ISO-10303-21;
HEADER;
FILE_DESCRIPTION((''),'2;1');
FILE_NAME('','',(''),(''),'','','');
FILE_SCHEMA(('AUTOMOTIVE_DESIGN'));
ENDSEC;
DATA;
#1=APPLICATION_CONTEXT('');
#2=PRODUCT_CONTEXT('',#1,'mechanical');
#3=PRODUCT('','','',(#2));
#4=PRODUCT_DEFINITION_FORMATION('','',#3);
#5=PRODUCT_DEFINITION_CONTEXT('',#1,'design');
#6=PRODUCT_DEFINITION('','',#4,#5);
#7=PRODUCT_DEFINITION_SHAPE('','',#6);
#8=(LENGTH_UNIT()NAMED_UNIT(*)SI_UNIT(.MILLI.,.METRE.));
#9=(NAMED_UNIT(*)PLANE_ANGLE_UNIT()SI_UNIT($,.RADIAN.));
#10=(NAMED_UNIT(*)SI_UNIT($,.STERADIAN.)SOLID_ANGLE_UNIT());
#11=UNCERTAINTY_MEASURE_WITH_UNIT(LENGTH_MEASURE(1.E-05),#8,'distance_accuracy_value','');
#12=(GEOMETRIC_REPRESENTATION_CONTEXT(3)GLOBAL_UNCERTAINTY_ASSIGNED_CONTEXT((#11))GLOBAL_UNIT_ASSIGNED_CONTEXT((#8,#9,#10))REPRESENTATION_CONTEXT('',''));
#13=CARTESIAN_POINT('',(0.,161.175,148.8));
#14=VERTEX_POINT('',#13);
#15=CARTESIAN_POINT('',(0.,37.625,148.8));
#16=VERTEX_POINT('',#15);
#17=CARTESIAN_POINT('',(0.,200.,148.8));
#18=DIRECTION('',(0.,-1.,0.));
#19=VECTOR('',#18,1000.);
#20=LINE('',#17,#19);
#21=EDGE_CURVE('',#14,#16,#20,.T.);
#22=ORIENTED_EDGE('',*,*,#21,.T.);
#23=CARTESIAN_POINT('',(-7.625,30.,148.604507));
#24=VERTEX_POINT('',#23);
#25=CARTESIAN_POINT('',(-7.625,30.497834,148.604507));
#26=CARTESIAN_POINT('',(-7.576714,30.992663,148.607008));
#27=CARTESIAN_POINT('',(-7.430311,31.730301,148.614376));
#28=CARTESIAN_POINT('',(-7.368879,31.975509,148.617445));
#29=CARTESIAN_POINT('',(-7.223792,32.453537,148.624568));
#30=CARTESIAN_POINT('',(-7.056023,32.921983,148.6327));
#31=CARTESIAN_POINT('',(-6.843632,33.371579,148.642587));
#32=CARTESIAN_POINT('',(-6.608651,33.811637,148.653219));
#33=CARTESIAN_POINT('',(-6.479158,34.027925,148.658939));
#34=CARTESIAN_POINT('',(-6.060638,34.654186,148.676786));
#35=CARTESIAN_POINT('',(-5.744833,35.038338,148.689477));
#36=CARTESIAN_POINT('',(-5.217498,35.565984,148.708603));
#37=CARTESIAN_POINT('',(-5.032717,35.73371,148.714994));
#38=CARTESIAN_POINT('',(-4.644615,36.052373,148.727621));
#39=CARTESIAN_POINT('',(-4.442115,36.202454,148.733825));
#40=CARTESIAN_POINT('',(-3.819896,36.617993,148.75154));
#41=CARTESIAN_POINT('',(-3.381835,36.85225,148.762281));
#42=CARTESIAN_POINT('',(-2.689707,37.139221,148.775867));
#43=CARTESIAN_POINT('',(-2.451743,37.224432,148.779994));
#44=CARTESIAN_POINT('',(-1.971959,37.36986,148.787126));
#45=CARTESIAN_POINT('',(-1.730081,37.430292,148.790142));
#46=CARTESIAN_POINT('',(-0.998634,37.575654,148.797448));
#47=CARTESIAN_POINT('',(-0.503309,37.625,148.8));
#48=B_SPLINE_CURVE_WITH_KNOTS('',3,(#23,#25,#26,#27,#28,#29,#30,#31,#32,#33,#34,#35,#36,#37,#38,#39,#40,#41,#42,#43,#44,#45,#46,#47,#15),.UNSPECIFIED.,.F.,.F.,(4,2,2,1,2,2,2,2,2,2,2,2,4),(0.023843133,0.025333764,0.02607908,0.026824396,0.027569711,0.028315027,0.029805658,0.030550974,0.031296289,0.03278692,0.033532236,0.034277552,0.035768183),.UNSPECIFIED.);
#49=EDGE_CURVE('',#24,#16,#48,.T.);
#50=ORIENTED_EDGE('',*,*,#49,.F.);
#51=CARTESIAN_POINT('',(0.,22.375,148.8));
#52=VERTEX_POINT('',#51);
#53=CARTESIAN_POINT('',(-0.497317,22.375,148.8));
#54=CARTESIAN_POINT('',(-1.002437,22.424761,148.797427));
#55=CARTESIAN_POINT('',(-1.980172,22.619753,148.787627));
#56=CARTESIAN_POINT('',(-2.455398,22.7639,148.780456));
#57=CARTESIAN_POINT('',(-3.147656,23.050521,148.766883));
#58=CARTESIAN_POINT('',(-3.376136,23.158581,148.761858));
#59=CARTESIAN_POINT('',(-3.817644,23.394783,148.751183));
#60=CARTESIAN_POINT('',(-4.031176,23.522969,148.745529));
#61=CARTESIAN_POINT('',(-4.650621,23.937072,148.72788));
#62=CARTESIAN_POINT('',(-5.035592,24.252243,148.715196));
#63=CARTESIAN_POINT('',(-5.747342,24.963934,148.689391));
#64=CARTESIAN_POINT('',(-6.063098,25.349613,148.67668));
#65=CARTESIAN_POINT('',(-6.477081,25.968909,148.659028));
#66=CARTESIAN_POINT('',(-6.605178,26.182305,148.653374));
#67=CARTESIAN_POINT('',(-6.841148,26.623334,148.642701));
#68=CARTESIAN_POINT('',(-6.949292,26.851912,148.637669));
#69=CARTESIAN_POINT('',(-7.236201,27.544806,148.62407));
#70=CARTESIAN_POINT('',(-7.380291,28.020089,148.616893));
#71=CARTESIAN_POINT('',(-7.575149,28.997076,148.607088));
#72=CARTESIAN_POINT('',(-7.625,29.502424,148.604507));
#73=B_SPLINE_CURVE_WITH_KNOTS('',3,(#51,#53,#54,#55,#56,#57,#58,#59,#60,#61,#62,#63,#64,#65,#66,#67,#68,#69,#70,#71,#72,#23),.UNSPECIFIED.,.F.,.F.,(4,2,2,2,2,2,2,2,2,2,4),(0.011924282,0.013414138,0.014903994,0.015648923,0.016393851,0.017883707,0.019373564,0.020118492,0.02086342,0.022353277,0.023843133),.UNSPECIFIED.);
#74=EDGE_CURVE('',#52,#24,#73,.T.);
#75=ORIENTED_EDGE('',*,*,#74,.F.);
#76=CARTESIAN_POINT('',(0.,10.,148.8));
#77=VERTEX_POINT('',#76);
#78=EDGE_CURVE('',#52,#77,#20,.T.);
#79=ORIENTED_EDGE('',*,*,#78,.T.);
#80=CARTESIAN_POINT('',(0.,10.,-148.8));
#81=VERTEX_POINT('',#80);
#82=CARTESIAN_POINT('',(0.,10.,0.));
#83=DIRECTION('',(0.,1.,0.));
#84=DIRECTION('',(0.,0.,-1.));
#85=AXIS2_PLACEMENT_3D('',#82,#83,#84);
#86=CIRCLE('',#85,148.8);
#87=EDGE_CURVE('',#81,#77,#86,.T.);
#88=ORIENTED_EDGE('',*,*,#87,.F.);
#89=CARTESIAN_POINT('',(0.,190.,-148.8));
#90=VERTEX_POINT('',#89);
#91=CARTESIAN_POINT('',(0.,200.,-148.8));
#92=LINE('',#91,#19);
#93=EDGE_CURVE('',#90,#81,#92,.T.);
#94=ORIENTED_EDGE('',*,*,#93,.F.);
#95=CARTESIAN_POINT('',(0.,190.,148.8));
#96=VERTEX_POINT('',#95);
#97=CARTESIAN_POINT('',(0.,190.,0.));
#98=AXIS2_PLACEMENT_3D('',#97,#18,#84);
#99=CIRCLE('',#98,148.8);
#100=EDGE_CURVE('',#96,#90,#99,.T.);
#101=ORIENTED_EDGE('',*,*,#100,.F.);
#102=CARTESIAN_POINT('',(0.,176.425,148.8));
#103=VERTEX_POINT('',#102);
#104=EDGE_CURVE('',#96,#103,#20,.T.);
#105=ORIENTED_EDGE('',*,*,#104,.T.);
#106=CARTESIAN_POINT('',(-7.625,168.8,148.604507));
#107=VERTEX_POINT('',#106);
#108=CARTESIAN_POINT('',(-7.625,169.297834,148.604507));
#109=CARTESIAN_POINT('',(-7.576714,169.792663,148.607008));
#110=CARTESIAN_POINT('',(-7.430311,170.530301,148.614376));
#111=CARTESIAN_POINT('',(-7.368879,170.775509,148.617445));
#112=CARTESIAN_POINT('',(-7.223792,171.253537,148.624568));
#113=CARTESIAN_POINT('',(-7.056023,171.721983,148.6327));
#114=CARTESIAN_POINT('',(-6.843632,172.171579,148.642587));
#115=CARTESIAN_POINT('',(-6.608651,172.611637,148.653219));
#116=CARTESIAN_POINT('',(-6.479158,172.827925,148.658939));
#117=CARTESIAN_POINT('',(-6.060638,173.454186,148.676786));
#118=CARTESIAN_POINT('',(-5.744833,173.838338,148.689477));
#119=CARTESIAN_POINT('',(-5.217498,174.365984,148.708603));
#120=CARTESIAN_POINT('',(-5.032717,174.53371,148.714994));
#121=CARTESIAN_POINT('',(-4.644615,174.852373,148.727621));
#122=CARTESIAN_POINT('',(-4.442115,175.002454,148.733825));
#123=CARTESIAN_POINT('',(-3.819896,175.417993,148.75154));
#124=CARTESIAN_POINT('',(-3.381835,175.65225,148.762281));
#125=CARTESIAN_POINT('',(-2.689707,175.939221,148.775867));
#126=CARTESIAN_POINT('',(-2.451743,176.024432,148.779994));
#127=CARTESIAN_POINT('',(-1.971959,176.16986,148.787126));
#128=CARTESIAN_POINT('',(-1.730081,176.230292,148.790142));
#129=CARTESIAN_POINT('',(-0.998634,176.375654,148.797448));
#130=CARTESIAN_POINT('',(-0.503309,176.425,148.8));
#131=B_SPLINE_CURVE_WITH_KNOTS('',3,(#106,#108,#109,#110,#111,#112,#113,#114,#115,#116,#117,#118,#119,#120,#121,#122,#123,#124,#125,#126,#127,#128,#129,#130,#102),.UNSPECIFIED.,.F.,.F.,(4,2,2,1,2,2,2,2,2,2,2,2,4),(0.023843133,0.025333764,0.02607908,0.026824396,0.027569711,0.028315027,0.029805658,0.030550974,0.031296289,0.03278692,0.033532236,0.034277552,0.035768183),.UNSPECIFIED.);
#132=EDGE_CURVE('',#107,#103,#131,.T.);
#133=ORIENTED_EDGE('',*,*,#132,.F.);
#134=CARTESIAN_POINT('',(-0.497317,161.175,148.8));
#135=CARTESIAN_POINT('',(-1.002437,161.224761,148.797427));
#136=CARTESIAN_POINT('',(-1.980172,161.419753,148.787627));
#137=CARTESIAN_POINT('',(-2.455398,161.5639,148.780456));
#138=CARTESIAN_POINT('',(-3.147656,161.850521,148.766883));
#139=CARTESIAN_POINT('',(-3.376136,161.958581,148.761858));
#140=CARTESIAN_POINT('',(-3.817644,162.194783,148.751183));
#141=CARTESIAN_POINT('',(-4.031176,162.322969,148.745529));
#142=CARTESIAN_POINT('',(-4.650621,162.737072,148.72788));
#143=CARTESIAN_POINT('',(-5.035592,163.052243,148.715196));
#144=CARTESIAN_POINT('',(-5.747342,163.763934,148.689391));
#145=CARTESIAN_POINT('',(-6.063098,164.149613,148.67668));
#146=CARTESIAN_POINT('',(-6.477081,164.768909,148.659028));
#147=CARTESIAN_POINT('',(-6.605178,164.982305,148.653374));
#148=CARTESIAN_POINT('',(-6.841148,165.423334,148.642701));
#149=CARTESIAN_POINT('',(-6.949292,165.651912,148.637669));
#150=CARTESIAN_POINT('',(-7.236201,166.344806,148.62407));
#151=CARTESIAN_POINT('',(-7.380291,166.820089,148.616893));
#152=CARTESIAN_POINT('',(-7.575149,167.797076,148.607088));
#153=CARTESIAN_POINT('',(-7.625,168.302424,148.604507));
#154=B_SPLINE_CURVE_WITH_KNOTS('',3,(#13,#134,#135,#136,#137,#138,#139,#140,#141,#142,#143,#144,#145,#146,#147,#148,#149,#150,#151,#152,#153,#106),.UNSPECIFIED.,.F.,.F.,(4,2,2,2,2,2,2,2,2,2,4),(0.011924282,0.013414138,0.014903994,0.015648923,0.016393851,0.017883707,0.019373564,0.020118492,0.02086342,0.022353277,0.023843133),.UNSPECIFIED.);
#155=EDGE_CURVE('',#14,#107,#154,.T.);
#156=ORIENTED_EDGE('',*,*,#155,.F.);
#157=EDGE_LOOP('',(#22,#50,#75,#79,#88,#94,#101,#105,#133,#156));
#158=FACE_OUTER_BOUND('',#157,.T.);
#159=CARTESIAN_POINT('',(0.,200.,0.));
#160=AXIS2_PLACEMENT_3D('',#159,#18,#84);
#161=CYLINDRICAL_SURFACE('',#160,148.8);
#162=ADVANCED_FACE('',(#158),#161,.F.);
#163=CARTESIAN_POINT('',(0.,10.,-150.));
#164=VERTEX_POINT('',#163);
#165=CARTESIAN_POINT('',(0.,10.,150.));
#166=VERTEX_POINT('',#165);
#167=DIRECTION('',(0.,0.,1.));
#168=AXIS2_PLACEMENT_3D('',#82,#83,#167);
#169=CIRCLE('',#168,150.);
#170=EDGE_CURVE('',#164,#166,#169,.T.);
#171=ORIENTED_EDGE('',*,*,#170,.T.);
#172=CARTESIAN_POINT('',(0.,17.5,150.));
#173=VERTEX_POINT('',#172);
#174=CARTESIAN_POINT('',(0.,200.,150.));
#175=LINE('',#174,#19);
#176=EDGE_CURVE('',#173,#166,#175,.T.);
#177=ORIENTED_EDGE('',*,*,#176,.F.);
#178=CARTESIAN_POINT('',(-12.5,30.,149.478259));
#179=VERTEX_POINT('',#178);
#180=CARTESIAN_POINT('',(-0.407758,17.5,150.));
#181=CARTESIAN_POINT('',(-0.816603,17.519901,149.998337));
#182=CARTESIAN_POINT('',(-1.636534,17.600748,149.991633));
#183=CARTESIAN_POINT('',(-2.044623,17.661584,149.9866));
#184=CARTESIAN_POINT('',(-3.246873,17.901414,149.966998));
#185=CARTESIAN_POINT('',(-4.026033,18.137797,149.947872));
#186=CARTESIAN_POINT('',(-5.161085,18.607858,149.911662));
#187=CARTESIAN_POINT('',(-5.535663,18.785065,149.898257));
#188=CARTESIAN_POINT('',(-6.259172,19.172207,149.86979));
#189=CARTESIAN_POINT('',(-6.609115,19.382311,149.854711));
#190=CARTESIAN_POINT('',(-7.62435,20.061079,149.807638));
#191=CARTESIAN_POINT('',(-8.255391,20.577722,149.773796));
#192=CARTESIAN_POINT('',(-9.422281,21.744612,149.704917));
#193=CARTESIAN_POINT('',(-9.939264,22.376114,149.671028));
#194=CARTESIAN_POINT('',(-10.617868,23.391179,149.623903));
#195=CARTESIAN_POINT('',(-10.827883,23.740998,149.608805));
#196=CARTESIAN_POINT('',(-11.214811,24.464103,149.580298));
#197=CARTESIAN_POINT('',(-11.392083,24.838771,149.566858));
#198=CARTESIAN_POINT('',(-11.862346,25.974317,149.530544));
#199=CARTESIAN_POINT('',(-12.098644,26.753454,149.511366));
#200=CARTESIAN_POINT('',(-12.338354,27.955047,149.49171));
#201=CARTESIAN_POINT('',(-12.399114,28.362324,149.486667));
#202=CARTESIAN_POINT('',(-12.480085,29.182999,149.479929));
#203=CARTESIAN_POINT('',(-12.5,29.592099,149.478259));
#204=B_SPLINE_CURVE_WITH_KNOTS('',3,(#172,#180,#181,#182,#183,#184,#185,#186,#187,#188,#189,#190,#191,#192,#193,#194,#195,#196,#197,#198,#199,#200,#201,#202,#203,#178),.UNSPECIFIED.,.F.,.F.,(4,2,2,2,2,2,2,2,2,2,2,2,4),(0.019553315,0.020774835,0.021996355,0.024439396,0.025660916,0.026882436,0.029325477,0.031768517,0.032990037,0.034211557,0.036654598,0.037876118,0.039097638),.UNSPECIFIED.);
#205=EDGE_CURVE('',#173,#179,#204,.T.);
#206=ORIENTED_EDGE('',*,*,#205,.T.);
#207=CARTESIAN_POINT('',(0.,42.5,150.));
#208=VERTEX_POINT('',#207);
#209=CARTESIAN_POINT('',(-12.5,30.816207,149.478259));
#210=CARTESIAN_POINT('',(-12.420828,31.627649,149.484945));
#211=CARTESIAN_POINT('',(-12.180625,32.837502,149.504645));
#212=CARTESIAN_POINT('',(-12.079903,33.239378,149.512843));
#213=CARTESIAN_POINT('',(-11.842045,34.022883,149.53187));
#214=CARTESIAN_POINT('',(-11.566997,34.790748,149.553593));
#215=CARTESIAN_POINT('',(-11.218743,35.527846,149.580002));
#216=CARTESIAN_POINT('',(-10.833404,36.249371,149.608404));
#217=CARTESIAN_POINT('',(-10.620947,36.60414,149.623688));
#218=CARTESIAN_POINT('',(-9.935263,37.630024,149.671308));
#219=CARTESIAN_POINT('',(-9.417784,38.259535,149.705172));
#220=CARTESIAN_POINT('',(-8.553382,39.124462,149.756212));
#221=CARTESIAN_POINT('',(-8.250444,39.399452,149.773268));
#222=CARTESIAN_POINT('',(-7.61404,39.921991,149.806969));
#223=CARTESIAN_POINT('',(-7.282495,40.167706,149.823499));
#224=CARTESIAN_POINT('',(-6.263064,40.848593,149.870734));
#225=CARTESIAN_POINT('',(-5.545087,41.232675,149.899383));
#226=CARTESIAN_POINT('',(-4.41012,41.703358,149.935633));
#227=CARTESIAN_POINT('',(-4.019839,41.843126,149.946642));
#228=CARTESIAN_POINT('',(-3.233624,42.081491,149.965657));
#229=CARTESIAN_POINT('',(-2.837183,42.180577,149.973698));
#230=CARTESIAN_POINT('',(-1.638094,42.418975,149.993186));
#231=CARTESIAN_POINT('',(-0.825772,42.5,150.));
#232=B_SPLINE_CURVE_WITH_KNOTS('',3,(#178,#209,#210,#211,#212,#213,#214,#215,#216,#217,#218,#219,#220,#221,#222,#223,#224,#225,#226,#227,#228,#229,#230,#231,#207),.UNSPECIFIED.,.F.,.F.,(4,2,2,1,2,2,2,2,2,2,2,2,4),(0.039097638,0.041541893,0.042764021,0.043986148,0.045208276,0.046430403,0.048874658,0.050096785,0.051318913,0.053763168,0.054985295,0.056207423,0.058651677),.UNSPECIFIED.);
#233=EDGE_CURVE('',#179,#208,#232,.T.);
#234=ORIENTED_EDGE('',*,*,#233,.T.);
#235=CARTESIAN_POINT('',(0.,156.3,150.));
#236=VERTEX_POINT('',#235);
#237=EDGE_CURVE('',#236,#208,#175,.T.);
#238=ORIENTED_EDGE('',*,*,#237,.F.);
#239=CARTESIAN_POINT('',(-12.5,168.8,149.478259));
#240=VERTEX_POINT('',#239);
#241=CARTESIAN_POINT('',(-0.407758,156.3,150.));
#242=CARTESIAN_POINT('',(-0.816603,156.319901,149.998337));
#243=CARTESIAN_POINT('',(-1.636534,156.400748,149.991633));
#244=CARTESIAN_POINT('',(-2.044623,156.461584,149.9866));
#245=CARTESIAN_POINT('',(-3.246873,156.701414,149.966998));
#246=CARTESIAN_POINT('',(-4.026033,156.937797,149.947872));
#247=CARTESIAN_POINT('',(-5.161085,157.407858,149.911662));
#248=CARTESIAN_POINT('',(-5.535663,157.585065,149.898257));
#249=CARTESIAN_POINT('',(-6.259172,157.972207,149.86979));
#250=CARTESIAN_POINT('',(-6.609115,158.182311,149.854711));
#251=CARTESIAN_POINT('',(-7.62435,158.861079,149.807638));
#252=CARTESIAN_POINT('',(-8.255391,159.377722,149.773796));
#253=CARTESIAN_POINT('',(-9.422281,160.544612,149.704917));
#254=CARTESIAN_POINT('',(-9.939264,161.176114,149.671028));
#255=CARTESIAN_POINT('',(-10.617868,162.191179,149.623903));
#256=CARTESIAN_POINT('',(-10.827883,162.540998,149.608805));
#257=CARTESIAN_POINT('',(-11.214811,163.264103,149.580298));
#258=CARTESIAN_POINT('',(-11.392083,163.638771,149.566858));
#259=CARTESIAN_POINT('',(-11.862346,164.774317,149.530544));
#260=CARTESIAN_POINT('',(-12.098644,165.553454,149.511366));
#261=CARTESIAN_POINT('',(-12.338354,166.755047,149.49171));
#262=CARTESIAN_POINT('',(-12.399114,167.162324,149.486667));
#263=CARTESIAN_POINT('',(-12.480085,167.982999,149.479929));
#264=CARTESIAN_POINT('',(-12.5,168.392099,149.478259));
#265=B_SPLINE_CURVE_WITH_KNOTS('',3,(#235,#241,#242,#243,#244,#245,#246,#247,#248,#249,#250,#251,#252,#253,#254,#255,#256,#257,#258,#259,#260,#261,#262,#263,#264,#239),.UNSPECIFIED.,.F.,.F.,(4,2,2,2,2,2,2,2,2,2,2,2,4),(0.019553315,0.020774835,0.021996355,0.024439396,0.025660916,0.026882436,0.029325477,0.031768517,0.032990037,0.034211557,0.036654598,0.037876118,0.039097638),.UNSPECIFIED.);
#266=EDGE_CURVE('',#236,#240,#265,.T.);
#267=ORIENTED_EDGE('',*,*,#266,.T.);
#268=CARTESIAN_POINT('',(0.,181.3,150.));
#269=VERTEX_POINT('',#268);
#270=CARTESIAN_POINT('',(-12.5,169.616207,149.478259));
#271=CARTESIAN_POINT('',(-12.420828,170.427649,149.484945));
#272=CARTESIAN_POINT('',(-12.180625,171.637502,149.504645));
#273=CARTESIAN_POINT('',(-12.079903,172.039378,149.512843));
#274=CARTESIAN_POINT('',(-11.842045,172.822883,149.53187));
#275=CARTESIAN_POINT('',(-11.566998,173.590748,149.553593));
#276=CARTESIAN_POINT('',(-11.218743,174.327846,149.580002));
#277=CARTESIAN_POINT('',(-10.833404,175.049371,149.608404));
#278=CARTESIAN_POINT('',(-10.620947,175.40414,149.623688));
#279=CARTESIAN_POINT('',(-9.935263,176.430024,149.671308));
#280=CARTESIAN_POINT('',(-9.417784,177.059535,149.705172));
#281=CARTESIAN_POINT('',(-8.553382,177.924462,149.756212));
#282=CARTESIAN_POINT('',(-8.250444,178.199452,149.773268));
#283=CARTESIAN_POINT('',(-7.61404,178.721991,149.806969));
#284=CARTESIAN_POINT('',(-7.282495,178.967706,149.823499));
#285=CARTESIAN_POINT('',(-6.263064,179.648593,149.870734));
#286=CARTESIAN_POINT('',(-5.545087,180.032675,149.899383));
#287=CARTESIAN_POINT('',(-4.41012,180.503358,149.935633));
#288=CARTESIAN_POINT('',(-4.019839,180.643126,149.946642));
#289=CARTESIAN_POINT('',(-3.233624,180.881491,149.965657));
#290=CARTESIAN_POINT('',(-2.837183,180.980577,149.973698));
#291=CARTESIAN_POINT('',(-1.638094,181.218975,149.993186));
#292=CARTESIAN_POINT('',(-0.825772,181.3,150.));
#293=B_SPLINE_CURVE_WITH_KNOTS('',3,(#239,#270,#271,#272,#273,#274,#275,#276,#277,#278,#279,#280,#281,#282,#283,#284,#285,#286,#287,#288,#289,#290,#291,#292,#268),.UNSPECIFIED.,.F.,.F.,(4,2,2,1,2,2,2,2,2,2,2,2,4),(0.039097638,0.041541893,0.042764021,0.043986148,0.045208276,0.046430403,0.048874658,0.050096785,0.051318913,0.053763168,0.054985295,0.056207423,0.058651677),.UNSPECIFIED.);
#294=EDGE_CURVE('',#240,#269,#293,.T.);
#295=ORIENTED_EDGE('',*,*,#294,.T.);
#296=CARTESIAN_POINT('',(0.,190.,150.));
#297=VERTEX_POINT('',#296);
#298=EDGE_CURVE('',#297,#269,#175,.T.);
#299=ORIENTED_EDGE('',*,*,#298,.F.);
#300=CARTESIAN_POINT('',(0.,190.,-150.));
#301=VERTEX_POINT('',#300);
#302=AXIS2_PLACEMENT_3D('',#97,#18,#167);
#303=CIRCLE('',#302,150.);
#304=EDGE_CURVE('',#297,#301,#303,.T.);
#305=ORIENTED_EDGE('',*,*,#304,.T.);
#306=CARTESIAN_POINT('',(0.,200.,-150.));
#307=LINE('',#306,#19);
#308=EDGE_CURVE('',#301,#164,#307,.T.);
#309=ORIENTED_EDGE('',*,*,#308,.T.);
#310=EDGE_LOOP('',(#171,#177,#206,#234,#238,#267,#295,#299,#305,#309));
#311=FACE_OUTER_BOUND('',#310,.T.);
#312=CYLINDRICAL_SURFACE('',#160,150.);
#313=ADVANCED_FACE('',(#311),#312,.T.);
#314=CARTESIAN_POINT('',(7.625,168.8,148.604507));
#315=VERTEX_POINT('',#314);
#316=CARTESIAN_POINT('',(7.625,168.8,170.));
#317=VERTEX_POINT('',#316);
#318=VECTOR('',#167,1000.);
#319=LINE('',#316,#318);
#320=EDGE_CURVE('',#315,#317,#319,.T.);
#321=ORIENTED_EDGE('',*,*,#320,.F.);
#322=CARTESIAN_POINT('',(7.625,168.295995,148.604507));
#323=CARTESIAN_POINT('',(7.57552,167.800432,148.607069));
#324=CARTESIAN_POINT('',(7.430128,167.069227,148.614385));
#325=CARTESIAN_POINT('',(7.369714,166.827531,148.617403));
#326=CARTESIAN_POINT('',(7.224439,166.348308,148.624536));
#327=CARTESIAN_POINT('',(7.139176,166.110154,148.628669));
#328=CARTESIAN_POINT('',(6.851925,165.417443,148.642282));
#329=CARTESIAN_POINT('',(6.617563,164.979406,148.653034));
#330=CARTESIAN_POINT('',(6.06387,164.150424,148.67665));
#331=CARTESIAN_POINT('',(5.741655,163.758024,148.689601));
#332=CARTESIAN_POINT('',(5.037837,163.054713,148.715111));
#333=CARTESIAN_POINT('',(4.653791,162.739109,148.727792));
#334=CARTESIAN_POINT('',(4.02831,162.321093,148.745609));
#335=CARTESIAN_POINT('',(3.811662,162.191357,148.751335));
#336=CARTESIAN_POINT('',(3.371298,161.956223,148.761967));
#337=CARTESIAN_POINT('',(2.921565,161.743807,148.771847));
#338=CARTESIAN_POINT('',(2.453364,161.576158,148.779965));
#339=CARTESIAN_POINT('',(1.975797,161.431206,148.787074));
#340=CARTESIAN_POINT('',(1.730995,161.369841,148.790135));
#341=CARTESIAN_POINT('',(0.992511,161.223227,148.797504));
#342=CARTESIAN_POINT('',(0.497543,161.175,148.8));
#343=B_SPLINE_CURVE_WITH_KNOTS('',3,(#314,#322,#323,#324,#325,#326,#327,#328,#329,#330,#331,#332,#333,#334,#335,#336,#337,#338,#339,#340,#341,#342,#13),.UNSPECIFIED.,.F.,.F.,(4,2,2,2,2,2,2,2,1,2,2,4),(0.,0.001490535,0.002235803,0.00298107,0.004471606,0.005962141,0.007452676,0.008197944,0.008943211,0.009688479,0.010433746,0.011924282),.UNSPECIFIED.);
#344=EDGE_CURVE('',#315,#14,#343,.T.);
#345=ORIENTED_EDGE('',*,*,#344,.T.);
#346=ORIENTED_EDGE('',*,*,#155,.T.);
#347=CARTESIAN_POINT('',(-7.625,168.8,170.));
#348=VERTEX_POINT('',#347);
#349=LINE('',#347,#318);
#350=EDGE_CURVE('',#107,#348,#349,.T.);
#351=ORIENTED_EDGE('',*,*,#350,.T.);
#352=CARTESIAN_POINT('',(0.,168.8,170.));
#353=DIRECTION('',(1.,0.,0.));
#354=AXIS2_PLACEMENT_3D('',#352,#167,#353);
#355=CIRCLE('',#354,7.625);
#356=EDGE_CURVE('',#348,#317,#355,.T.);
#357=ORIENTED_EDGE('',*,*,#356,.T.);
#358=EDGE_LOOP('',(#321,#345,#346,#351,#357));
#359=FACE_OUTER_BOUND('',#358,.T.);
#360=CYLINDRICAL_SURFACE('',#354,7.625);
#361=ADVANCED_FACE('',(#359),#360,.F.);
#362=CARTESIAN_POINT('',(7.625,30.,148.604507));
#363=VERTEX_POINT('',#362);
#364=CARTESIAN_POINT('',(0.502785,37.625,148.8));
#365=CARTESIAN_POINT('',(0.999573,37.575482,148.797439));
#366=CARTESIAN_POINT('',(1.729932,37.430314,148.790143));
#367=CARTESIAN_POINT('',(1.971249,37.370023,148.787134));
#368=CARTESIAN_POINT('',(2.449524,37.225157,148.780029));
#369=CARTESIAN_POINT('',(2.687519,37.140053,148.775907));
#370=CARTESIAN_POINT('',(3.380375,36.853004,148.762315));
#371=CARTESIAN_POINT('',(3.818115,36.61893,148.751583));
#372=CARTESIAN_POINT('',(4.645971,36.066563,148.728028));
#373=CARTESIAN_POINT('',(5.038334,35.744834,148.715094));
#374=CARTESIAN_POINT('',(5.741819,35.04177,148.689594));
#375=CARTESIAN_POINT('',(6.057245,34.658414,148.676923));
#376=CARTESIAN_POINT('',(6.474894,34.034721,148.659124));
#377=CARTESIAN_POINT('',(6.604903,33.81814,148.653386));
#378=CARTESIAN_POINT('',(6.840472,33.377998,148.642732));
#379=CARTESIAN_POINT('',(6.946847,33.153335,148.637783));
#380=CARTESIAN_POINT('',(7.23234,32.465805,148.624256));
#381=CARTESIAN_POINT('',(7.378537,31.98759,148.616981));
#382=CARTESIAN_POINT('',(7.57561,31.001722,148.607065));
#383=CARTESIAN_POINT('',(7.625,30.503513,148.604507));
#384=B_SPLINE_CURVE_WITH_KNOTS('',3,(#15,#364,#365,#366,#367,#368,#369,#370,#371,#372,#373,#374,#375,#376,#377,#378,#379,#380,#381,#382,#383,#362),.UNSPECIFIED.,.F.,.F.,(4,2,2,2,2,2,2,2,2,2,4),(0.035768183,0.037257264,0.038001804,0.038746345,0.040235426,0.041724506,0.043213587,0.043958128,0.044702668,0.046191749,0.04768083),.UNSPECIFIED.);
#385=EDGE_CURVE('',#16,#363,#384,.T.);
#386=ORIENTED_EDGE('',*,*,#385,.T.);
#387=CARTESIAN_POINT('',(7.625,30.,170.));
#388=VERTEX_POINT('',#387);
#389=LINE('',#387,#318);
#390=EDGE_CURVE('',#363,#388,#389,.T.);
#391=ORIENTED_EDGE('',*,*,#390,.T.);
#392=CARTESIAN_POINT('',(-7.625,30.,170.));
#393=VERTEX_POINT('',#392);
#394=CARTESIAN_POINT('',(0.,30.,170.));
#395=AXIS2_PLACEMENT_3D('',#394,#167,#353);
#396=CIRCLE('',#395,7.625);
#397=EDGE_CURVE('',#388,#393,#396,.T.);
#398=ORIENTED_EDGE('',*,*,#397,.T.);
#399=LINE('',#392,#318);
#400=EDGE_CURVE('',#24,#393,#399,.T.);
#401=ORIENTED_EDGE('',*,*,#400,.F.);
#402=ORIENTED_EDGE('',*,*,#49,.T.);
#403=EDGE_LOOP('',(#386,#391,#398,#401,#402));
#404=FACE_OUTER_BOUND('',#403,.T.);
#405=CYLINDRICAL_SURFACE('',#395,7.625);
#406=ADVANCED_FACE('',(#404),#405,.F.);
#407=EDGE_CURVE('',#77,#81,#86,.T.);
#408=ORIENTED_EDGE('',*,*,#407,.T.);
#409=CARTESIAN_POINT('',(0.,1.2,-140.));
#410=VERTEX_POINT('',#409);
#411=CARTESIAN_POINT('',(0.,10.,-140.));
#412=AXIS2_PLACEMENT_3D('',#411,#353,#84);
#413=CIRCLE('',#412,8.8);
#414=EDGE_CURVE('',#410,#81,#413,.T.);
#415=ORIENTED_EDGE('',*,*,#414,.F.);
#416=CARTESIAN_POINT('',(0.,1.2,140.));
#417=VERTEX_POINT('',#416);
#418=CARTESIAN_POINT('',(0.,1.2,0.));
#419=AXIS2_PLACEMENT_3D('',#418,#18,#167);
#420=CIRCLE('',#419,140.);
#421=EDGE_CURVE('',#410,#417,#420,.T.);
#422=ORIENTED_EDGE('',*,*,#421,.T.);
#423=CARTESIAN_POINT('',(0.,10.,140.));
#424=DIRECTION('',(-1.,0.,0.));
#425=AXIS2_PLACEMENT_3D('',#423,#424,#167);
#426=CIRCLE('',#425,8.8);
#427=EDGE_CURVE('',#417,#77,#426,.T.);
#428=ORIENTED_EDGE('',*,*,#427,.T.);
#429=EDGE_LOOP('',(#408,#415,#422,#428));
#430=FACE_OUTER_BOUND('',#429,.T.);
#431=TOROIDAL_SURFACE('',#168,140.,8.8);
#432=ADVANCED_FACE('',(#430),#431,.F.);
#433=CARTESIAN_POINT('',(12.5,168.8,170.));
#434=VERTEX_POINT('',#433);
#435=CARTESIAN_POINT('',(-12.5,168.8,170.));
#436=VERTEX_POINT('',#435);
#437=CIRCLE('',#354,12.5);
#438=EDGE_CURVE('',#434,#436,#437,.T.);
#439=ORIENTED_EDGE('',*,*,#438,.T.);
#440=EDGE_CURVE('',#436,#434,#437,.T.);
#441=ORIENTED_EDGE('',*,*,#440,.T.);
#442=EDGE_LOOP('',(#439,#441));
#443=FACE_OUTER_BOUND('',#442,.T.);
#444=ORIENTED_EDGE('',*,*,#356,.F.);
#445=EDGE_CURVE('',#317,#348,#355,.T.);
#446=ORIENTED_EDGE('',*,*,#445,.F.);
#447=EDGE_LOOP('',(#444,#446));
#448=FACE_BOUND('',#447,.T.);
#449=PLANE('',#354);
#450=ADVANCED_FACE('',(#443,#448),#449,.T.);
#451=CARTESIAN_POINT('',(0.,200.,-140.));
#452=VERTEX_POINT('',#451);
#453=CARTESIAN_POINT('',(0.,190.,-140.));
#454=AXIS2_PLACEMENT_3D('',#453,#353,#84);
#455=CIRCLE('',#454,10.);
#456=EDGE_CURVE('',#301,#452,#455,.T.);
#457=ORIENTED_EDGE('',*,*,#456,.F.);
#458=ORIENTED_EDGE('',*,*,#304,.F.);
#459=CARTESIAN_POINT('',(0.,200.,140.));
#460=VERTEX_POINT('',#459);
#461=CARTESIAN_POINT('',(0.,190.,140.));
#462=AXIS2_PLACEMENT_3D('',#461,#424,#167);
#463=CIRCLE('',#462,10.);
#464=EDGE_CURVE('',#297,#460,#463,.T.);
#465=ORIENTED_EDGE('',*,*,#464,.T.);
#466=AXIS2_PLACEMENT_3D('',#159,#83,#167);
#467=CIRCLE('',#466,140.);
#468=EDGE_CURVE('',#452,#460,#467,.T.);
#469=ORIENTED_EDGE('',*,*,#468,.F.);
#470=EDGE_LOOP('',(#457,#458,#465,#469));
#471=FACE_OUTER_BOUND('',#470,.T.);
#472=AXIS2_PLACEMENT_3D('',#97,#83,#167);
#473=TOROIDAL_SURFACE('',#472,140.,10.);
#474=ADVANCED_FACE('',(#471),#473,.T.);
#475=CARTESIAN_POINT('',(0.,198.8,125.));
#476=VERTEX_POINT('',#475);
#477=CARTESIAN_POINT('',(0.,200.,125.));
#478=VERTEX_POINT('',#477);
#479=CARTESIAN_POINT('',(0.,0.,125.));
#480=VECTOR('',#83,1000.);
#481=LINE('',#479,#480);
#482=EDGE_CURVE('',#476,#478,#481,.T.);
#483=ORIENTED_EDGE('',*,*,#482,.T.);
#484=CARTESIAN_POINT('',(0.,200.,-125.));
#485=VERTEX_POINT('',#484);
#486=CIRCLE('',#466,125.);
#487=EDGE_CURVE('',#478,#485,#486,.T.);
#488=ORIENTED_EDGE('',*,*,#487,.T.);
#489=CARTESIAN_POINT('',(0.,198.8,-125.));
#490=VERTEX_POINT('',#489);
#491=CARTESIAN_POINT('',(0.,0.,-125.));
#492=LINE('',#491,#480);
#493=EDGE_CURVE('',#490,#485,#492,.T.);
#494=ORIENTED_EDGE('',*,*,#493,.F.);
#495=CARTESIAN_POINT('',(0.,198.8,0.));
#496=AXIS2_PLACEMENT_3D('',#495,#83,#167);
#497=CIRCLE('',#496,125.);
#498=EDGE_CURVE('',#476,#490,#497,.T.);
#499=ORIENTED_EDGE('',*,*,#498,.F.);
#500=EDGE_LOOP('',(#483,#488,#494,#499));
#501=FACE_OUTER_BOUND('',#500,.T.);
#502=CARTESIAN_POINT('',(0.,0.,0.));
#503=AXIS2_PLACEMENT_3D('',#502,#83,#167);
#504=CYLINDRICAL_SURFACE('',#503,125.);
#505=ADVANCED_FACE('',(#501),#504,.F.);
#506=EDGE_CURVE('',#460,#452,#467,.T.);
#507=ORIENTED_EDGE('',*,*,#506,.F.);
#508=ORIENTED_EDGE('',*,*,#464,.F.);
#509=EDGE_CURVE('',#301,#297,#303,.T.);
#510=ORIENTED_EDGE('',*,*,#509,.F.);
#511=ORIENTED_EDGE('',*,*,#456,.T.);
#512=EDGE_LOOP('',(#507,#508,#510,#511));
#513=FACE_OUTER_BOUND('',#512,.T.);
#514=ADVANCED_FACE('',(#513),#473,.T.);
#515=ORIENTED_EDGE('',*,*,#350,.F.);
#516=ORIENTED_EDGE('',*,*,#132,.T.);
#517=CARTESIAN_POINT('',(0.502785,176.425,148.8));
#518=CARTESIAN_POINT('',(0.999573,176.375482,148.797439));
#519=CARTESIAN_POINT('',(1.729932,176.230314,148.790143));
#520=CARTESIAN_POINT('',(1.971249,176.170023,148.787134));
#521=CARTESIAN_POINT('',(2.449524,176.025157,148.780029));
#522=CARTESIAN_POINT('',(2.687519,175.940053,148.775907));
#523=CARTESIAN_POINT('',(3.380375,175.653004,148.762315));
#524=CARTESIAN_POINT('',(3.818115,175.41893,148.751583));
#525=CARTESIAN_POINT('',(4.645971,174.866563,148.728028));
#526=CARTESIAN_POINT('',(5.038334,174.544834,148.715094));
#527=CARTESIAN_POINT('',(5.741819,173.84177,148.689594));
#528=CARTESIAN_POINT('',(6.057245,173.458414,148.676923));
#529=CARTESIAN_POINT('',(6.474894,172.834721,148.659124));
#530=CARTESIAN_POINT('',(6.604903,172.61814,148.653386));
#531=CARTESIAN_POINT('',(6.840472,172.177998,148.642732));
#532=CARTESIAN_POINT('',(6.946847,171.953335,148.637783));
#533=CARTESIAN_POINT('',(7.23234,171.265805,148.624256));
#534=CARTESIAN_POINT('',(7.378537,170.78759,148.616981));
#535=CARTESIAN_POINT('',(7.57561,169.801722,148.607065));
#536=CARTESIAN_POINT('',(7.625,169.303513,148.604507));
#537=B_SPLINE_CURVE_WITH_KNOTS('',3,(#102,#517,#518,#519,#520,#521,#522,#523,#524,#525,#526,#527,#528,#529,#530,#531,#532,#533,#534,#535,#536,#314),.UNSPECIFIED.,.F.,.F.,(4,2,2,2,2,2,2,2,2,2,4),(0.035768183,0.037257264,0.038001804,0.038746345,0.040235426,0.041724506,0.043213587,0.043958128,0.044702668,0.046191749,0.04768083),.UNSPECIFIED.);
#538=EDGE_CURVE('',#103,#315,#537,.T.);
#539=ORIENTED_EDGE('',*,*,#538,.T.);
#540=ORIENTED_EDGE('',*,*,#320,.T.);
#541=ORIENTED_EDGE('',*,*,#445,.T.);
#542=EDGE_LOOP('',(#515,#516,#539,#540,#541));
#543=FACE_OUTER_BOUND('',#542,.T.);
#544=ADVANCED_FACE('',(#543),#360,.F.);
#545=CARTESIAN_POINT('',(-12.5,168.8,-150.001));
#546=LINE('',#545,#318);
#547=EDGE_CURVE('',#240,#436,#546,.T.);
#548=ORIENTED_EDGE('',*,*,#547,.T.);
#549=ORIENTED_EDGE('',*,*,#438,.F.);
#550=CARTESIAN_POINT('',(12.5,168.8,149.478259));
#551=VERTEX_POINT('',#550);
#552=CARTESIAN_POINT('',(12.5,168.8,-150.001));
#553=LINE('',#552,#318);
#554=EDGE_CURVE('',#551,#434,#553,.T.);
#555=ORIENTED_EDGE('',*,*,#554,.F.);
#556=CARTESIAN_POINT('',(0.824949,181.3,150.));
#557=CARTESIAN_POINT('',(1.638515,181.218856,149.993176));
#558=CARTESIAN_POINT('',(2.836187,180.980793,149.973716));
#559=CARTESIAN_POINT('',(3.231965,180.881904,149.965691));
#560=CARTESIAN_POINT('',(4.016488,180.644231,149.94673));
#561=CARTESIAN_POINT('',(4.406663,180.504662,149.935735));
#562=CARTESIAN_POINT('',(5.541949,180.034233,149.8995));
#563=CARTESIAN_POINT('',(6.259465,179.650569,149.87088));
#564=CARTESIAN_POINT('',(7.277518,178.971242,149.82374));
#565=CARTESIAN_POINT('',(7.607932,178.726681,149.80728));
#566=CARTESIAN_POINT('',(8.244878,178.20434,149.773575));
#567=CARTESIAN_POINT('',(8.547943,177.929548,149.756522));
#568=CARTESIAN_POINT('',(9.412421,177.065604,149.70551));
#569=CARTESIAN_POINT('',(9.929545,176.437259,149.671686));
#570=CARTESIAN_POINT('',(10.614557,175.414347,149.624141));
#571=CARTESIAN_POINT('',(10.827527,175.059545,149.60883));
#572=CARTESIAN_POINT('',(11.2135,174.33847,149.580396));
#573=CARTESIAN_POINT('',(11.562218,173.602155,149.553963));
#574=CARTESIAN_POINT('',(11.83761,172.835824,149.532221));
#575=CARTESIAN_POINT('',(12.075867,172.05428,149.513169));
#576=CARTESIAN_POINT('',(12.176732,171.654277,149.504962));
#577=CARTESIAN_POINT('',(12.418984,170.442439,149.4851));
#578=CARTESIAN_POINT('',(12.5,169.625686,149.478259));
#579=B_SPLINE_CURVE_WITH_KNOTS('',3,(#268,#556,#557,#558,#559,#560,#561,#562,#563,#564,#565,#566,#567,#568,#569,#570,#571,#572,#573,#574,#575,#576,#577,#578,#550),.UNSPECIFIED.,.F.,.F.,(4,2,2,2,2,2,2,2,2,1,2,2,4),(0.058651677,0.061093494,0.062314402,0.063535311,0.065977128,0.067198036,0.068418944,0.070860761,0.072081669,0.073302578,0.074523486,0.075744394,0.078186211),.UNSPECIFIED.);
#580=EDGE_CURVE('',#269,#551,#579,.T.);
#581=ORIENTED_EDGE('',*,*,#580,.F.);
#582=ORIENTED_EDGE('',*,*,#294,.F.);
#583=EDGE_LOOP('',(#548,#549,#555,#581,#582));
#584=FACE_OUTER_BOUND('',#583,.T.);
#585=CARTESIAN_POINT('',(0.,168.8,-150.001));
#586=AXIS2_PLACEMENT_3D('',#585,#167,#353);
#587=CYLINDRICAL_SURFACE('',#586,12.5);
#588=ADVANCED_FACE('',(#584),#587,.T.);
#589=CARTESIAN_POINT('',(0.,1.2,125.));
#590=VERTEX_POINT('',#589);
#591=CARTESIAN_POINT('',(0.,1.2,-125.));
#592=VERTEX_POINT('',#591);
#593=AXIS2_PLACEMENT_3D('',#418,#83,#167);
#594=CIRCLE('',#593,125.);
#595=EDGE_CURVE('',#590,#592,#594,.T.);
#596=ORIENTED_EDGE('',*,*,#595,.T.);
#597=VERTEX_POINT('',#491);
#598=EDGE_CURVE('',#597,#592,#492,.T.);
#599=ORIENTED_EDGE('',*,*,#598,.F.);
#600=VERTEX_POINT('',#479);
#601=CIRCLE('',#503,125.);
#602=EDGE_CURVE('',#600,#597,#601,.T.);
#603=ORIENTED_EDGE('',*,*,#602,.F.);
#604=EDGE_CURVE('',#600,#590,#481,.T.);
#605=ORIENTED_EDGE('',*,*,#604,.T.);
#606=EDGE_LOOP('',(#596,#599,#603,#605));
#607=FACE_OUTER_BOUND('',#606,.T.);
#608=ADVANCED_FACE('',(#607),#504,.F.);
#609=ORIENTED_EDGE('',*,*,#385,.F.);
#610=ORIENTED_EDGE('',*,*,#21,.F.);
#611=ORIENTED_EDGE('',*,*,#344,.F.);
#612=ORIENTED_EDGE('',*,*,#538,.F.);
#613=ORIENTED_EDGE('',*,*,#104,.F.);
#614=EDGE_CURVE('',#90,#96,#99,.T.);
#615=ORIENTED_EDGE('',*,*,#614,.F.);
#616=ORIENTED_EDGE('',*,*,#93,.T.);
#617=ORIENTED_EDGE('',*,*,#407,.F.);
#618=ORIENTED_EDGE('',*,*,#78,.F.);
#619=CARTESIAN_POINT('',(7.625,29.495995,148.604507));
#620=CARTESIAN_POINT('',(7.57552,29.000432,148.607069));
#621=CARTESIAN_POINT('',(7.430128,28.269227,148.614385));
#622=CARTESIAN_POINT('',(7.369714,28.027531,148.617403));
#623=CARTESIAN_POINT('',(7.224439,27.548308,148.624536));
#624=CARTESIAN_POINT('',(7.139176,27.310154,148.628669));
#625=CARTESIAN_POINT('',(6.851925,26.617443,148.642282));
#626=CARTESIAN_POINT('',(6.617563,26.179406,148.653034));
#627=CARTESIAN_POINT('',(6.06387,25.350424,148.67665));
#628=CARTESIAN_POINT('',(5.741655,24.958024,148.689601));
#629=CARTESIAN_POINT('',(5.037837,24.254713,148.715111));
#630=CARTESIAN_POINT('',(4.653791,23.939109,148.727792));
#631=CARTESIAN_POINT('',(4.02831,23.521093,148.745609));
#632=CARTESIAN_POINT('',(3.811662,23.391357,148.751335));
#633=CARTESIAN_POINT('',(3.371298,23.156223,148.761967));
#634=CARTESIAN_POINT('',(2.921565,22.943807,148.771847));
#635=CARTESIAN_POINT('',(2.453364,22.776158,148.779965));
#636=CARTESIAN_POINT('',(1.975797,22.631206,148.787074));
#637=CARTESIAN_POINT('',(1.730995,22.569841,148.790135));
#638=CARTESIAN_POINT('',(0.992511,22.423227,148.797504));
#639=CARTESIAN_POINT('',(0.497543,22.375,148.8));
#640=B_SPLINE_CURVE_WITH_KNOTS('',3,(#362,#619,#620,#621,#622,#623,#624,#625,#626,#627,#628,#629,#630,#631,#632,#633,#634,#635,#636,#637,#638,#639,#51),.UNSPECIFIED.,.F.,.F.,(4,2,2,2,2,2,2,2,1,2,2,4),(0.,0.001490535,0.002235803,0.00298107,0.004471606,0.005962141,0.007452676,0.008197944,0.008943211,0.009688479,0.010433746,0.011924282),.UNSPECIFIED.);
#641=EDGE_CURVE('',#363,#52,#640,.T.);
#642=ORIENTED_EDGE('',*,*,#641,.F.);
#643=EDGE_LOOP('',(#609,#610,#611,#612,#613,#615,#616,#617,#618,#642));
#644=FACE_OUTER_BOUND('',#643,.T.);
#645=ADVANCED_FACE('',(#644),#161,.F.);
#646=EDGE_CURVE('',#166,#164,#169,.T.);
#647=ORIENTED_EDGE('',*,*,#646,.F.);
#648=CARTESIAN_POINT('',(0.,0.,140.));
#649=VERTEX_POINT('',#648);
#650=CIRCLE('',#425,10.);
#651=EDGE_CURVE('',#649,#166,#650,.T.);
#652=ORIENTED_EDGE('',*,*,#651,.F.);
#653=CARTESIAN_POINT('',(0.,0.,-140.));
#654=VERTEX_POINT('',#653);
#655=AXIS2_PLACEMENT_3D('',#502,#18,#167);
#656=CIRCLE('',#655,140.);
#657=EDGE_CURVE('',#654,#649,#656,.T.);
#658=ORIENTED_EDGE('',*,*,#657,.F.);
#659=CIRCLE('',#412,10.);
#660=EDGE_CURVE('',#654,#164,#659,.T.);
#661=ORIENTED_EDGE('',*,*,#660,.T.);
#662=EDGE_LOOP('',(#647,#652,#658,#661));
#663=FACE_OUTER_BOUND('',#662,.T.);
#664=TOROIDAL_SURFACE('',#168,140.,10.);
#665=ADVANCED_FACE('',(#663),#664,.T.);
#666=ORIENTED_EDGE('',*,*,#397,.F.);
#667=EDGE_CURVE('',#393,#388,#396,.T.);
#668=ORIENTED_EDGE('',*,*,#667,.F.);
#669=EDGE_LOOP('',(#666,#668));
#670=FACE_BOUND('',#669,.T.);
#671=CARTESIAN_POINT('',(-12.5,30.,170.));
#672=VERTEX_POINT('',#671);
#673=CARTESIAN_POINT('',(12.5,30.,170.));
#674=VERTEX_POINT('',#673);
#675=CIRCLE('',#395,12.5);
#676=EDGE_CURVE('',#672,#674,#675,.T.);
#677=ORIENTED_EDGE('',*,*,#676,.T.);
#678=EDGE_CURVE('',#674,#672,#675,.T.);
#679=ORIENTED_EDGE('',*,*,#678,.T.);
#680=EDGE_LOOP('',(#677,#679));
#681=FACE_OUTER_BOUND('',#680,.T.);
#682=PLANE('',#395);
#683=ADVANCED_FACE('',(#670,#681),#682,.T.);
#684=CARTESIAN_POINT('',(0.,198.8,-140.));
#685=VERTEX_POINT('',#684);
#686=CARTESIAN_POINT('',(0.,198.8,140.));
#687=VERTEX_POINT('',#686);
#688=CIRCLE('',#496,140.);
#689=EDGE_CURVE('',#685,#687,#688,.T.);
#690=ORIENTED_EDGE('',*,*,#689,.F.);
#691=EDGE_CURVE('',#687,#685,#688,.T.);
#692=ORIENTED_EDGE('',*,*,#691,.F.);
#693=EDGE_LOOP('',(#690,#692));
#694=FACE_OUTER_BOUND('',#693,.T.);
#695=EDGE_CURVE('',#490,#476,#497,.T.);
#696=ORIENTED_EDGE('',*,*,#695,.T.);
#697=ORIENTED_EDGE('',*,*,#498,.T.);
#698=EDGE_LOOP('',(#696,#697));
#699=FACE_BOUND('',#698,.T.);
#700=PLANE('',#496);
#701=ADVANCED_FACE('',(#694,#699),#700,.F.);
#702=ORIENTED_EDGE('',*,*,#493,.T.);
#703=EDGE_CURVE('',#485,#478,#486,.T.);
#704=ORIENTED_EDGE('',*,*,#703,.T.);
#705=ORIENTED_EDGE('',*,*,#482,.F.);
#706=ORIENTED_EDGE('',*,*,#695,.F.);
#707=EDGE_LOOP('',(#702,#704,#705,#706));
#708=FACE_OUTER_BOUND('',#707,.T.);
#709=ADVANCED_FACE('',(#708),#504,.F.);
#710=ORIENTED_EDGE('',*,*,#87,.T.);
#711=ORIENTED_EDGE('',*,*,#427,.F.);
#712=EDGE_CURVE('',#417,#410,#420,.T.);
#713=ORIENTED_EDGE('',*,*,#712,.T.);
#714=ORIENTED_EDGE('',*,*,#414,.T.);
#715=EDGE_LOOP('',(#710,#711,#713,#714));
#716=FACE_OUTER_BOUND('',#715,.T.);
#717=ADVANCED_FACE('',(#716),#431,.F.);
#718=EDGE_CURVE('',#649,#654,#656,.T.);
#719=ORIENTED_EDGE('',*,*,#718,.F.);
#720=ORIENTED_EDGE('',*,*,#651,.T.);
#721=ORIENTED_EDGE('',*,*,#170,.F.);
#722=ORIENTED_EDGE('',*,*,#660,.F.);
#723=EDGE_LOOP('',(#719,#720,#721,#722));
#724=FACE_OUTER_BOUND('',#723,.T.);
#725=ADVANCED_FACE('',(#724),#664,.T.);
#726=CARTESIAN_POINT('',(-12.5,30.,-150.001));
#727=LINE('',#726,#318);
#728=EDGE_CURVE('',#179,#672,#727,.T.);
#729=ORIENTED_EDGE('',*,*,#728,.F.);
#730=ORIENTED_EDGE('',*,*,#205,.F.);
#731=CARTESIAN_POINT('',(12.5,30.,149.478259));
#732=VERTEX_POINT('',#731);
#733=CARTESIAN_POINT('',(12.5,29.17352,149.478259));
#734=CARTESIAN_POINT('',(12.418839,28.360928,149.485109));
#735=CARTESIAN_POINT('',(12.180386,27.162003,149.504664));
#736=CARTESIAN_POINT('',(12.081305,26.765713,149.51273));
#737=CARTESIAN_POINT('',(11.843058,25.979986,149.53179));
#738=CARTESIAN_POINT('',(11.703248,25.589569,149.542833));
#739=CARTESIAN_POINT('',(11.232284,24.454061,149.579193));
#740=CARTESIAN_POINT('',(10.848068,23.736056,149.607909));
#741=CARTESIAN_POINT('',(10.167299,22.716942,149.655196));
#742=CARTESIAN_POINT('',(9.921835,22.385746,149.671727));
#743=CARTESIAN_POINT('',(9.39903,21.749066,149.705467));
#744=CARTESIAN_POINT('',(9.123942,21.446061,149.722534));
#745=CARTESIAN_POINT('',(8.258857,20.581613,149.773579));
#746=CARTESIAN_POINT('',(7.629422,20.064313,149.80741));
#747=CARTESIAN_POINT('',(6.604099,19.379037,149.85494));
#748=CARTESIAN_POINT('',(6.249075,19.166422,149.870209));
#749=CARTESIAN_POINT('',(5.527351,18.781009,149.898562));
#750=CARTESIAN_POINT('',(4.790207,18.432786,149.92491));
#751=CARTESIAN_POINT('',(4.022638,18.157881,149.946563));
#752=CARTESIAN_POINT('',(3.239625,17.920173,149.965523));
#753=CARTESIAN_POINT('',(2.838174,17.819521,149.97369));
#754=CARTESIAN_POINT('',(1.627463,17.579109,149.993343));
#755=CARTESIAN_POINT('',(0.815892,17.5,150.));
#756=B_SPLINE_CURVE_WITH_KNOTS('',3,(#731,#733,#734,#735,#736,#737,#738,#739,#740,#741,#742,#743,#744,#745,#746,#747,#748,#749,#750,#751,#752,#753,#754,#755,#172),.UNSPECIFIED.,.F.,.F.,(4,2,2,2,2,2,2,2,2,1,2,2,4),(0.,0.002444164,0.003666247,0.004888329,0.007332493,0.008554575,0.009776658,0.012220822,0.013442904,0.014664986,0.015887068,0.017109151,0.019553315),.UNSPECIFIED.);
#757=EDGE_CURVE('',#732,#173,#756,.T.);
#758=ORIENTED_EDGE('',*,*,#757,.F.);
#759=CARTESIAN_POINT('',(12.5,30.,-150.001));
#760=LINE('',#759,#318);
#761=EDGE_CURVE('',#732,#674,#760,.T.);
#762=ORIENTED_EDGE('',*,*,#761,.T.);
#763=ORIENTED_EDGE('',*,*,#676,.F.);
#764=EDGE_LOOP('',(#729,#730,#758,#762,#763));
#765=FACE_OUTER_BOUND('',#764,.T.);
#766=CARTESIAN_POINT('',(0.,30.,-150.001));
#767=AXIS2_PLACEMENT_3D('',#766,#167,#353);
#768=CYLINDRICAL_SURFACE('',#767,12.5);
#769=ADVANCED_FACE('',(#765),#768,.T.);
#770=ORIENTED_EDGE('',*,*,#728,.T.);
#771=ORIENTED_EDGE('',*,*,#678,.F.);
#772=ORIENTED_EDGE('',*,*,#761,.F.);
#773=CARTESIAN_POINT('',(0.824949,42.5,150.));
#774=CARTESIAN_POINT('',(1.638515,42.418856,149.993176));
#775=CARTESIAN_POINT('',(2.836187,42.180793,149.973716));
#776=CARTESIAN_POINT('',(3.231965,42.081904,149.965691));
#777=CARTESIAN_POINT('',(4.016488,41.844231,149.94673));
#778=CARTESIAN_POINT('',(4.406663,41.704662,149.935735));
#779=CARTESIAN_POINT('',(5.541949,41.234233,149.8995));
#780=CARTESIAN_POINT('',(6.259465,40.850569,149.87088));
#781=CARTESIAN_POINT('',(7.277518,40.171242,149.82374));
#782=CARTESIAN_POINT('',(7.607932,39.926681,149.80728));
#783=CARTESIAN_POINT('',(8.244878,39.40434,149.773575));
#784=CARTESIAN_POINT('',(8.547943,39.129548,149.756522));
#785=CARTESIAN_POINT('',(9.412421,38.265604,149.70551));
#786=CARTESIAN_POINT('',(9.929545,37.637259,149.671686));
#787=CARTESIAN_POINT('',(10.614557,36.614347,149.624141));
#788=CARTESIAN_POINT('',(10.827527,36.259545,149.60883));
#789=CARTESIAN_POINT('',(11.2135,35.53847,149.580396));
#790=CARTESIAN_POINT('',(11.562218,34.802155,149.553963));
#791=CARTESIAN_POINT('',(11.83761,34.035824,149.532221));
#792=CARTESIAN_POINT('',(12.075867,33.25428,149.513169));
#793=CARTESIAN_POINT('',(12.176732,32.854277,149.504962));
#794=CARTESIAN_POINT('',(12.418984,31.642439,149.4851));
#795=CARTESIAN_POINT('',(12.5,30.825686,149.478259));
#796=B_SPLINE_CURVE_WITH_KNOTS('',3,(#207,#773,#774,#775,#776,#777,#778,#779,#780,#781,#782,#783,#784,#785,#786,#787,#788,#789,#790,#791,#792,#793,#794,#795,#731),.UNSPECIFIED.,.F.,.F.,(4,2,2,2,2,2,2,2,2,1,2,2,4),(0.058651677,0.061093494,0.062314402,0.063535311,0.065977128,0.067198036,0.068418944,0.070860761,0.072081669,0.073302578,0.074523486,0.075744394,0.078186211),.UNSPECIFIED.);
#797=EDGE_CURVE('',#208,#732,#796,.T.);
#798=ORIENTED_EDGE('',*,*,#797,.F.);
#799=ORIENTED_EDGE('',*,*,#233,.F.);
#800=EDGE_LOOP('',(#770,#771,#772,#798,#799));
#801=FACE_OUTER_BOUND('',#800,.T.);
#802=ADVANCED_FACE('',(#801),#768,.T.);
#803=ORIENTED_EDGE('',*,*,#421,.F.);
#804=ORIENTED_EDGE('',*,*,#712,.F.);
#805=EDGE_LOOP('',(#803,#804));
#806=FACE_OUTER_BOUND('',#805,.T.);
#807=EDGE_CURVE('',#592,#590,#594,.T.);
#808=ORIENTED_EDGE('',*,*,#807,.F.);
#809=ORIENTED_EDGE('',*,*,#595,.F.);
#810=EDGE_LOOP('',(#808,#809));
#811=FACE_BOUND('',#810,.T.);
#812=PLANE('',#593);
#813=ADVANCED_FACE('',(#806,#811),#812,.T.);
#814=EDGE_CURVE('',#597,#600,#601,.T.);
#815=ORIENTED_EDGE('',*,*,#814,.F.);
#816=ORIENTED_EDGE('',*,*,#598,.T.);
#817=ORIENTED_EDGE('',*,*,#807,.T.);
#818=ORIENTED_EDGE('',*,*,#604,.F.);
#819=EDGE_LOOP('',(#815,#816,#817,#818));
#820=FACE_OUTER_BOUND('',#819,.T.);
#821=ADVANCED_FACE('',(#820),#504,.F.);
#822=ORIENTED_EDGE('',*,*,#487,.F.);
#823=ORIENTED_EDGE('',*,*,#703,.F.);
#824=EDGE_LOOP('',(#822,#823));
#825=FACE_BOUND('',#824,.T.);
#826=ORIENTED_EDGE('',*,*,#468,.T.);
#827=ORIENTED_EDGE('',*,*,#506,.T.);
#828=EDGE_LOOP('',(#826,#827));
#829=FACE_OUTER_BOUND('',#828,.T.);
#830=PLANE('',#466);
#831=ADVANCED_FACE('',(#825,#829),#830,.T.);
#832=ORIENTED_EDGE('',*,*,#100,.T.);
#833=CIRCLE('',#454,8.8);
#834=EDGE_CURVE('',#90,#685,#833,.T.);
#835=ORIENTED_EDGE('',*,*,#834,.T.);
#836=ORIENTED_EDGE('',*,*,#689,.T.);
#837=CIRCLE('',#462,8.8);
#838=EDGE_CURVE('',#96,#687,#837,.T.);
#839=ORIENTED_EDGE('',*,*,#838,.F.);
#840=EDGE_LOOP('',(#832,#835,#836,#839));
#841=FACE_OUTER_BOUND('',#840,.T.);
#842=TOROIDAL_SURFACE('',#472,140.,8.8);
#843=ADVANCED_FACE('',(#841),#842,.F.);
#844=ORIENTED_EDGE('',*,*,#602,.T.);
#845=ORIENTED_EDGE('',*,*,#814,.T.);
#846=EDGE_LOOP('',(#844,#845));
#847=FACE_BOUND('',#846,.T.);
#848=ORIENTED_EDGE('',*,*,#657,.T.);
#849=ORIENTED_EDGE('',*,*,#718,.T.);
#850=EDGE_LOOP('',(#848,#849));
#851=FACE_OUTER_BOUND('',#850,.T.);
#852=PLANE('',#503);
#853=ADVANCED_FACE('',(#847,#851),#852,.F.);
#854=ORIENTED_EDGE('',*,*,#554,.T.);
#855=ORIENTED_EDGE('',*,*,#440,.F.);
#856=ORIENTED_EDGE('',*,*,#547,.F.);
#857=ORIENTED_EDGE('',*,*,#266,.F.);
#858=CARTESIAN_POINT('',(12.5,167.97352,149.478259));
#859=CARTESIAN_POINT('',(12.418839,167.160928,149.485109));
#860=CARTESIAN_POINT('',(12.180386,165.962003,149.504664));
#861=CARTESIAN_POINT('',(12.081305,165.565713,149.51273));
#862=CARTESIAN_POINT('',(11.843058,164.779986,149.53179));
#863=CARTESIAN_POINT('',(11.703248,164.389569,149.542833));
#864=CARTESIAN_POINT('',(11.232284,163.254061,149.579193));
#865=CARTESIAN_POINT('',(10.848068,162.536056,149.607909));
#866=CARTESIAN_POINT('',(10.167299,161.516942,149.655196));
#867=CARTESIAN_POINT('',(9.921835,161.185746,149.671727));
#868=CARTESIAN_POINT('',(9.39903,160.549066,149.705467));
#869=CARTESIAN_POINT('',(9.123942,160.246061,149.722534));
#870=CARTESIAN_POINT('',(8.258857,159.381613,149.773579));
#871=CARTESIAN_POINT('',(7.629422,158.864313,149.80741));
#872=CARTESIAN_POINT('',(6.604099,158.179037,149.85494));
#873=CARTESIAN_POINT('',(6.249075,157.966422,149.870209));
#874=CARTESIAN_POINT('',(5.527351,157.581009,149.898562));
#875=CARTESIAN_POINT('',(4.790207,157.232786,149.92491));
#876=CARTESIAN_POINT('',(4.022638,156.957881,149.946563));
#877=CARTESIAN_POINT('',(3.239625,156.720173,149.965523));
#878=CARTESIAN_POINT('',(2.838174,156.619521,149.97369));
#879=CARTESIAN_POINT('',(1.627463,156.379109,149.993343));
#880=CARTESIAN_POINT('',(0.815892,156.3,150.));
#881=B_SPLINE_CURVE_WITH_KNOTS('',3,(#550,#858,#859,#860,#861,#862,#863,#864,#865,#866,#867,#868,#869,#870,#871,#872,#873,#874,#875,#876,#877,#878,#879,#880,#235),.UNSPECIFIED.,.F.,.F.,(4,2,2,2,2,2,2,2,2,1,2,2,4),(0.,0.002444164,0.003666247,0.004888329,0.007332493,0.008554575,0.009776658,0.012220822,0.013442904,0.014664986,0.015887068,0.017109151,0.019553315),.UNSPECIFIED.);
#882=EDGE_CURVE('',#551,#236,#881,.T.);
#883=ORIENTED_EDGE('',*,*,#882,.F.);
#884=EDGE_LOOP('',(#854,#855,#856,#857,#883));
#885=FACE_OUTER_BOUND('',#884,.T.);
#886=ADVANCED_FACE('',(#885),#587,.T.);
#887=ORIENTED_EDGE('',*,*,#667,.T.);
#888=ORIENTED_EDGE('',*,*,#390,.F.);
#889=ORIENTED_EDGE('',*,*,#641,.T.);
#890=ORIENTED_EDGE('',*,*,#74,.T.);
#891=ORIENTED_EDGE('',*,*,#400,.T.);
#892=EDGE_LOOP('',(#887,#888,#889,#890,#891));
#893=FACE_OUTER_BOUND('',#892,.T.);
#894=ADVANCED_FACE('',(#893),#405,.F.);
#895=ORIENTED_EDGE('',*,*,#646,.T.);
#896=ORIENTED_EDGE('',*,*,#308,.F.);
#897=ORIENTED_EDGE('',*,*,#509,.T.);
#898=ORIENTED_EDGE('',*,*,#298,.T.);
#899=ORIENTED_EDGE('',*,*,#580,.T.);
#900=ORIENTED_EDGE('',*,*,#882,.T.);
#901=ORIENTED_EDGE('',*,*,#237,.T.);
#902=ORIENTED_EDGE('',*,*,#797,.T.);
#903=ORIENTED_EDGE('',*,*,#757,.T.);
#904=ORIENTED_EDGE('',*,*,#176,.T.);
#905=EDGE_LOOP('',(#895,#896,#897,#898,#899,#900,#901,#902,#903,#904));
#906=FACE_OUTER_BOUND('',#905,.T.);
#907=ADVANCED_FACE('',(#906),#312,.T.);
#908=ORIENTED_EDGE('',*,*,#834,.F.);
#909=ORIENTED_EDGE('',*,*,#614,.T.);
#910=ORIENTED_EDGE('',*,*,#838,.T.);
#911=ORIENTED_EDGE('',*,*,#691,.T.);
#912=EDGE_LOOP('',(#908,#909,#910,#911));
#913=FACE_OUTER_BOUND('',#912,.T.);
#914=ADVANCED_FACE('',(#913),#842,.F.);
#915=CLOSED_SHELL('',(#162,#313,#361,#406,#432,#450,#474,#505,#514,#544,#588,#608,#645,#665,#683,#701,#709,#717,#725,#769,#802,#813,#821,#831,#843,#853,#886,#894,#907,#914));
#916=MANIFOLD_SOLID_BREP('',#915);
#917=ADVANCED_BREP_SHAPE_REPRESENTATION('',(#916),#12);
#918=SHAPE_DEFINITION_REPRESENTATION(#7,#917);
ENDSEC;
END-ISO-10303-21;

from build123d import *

# Parameters (mm, degrees)
SKETCH1_R                = 150
BOSS_EXTRUDE1_DEPTH      = 200
FILLET1_R                = 10
SKETCH2_R                = 125
CUT_EXTRUDE1_DEPTH       = 292.547594794
SHELL2_T                 = -1.2
BOSS_EXTRUDE2_REACH      = 408.079
BOSS_EXTRUDE2_END_RADIUS = 150
SKETCH5_R                = 12.5
G3_8_TAPPED_HOLE1_D      = 15.25
G3_8_TAPPED_HOLE1_DEPTH  = 37.33
G3_8_TAPPED_HOLE1_TIP    = 4.58156222


with BuildPart() as part:
    # Sketch1 → Boss-Extrude1 (new body)
    with BuildSketch(Plane(origin=(0, 0, 0), x_dir=(1, 0, 0), z_dir=(0, 1, 0))):
        with Locations(Location((0, 0, 0), (0, 0, 270))):
            Circle(SKETCH1_R)
    extrude(amount=BOSS_EXTRUDE1_DEPTH)

    # Fillet1
    fillet1_edges = [part.edges().sort_by_distance(p)[0] for p in [
        (0, 0, -150),
        (0, 200, -150),
    ]]
    fillet(fillet1_edges, radius=FILLET1_R)

    # Sketch2 → Cut-Extrude1 (cut, through all)
    with BuildSketch(Plane(origin=(0, 200, 0), x_dir=(1, 0, 0), z_dir=(0, 1, 0))):
        with Locations(Location((0, 0, 0), (0, 0, 270))):
            Circle(SKETCH2_R)
    extrude(amount=-CUT_EXTRUDE1_DEPTH, mode=Mode.SUBTRACT)

    # Shell2
    shell2_openings = [part.faces().sort_by_distance(p)[0] for p in [
        (0, 100, -125),
    ]]
    offset(amount=SHELL2_T, openings=shell2_openings, kind=Kind.INTERSECTION)

    # Boss-Extrude2: up to this cylinder (the profile starts outside it)
    boss_extrude2_end = Plane(origin=(0, 99.4, 0), z_dir=(0, -1, 0)) * Cylinder(BOSS_EXTRUDE2_END_RADIUS, 1255.958, mode=Mode.PRIVATE)
    # Sketch5 → Boss-Extrude2 (add, up to the surface)
    with BuildSketch(Plane.XY.offset(170), mode=Mode.PRIVATE) as boss_extrude2_sk1:
        with Locations((0, 30)):
            Circle(SKETCH5_R)
    boss_extrude2_tool1 = extrude(boss_extrude2_sk1.sketch, amount=-BOSS_EXTRUDE2_REACH, mode=Mode.PRIVATE) - boss_extrude2_end
    add(boss_extrude2_tool1.solids().sort_by_distance((0, 30, 170))[0])
    # Sketch5 → Boss-Extrude2 (add, up to the surface)
    with BuildSketch(Plane.XY.offset(170), mode=Mode.PRIVATE) as boss_extrude2_sk2:
        with Locations((0, 168.8)):
            Circle(SKETCH5_R)
    boss_extrude2_tool2 = extrude(boss_extrude2_sk2.sketch, amount=-BOSS_EXTRUDE2_REACH, mode=Mode.PRIVATE) - boss_extrude2_end
    add(boss_extrude2_tool2.solids().sort_by_distance((0, 168.8, 170))[0])

    # G3/8 Tapped Hole1
    with Locations(Plane(origin=(0, 30, 170), x_dir=(1, 0, 0), z_dir=(0, 0, 1))):
        with Locations((0, 0), (0, 138.8)):
            Hole(G3_8_TAPPED_HOLE1_D / 2, depth=G3_8_TAPPED_HOLE1_DEPTH)
            with Locations((0, 0, -(G3_8_TAPPED_HOLE1_DEPTH + G3_8_TAPPED_HOLE1_TIP / 2))):  # 118° drill point
                Cone(0, G3_8_TAPPED_HOLE1_D / 2, G3_8_TAPPED_HOLE1_TIP, mode=Mode.SUBTRACT)


solid = part.part
